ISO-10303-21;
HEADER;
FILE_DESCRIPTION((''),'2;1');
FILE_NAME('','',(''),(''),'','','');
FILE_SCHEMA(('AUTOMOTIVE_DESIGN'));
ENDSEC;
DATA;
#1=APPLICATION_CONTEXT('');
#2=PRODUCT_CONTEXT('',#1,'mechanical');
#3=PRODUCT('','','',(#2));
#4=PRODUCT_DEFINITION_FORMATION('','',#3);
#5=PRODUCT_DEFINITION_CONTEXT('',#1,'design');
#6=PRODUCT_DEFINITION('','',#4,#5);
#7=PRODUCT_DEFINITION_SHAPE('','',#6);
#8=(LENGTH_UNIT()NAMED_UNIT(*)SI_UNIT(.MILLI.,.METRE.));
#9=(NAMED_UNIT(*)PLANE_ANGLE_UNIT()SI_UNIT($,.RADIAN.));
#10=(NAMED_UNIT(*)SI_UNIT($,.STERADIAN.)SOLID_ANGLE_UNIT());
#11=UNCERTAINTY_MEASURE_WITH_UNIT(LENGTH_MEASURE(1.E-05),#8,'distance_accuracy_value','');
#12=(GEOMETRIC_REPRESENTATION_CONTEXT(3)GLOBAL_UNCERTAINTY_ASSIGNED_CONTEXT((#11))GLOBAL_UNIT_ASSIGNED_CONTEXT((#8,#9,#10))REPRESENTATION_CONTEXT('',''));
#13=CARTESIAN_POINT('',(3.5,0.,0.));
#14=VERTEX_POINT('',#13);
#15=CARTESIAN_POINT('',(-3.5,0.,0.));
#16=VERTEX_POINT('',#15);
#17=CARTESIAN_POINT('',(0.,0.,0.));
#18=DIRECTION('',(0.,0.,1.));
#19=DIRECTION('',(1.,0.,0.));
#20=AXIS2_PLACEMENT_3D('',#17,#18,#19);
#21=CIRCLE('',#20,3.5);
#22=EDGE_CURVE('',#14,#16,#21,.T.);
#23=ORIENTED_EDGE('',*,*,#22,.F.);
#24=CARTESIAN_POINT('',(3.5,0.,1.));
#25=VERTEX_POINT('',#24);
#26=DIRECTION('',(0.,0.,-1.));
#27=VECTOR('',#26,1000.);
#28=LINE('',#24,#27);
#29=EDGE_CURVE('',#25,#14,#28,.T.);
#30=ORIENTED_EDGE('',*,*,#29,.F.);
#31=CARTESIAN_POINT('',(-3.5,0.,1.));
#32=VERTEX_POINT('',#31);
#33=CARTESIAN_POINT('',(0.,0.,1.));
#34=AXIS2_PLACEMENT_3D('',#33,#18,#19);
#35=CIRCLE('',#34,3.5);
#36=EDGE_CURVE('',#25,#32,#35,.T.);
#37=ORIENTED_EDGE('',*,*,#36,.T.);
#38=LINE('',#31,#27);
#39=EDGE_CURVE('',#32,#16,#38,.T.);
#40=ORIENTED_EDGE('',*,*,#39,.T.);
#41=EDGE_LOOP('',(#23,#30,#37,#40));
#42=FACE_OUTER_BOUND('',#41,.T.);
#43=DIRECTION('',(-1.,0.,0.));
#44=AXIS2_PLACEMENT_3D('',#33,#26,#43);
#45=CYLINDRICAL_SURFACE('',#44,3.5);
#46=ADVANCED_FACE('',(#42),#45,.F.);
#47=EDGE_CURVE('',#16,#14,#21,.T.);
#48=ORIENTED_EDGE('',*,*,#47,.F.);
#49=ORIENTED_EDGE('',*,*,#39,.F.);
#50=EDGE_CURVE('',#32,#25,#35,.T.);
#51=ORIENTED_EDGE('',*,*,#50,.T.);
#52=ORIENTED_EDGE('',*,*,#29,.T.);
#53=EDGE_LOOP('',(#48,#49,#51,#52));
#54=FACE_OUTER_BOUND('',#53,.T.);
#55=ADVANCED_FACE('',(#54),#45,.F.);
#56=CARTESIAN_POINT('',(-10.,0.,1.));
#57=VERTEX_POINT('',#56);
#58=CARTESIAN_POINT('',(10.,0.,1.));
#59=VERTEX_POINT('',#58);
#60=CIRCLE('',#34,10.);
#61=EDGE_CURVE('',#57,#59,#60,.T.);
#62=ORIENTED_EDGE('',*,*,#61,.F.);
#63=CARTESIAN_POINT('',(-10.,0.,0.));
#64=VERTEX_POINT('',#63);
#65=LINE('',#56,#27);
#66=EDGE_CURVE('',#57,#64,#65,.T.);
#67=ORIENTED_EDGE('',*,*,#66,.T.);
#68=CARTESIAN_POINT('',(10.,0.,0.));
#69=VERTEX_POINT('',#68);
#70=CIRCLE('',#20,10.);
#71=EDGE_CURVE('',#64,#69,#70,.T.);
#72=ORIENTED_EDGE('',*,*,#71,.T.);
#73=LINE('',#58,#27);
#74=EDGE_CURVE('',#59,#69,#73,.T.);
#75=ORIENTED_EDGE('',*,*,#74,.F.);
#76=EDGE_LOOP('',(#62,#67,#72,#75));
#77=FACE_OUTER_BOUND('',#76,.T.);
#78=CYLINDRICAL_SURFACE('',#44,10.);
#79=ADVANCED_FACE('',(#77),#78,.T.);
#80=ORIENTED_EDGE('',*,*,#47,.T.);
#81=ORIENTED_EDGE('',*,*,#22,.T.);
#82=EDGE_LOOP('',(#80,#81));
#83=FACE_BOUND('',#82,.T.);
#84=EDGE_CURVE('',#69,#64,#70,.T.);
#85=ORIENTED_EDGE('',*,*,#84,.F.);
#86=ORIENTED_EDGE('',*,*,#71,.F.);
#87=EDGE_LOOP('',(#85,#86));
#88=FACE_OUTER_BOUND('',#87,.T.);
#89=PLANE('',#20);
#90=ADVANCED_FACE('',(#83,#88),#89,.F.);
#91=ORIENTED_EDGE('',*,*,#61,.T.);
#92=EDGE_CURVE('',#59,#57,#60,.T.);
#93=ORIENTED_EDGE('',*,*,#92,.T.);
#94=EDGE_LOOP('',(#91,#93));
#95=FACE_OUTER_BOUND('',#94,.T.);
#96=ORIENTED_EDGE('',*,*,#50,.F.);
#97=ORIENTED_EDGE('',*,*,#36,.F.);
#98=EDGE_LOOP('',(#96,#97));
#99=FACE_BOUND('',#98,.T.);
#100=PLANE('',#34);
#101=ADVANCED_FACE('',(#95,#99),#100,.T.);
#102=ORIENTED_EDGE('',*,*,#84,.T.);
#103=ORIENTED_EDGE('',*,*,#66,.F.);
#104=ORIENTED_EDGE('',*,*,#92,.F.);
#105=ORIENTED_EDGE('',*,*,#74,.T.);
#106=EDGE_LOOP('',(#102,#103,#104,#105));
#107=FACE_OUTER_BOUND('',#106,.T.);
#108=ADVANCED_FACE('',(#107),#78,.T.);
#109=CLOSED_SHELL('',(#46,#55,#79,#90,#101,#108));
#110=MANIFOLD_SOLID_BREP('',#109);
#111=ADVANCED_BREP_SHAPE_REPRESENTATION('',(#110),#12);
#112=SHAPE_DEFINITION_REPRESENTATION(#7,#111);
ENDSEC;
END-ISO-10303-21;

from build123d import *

# Parameters (mm, degrees)
SKETCH1_R           = 10
SKETCH1_R_2         = 3.5
BOSS_EXTRUDE1_DEPTH = 1


with BuildPart() as part:
    # Sketch1 → Boss-Extrude1 (new body)
    with BuildSketch(Plane.XY):
        Circle(SKETCH1_R)
        Circle(SKETCH1_R_2, mode=Mode.SUBTRACT)
    extrude(amount=BOSS_EXTRUDE1_DEPTH)


solid = part.part
